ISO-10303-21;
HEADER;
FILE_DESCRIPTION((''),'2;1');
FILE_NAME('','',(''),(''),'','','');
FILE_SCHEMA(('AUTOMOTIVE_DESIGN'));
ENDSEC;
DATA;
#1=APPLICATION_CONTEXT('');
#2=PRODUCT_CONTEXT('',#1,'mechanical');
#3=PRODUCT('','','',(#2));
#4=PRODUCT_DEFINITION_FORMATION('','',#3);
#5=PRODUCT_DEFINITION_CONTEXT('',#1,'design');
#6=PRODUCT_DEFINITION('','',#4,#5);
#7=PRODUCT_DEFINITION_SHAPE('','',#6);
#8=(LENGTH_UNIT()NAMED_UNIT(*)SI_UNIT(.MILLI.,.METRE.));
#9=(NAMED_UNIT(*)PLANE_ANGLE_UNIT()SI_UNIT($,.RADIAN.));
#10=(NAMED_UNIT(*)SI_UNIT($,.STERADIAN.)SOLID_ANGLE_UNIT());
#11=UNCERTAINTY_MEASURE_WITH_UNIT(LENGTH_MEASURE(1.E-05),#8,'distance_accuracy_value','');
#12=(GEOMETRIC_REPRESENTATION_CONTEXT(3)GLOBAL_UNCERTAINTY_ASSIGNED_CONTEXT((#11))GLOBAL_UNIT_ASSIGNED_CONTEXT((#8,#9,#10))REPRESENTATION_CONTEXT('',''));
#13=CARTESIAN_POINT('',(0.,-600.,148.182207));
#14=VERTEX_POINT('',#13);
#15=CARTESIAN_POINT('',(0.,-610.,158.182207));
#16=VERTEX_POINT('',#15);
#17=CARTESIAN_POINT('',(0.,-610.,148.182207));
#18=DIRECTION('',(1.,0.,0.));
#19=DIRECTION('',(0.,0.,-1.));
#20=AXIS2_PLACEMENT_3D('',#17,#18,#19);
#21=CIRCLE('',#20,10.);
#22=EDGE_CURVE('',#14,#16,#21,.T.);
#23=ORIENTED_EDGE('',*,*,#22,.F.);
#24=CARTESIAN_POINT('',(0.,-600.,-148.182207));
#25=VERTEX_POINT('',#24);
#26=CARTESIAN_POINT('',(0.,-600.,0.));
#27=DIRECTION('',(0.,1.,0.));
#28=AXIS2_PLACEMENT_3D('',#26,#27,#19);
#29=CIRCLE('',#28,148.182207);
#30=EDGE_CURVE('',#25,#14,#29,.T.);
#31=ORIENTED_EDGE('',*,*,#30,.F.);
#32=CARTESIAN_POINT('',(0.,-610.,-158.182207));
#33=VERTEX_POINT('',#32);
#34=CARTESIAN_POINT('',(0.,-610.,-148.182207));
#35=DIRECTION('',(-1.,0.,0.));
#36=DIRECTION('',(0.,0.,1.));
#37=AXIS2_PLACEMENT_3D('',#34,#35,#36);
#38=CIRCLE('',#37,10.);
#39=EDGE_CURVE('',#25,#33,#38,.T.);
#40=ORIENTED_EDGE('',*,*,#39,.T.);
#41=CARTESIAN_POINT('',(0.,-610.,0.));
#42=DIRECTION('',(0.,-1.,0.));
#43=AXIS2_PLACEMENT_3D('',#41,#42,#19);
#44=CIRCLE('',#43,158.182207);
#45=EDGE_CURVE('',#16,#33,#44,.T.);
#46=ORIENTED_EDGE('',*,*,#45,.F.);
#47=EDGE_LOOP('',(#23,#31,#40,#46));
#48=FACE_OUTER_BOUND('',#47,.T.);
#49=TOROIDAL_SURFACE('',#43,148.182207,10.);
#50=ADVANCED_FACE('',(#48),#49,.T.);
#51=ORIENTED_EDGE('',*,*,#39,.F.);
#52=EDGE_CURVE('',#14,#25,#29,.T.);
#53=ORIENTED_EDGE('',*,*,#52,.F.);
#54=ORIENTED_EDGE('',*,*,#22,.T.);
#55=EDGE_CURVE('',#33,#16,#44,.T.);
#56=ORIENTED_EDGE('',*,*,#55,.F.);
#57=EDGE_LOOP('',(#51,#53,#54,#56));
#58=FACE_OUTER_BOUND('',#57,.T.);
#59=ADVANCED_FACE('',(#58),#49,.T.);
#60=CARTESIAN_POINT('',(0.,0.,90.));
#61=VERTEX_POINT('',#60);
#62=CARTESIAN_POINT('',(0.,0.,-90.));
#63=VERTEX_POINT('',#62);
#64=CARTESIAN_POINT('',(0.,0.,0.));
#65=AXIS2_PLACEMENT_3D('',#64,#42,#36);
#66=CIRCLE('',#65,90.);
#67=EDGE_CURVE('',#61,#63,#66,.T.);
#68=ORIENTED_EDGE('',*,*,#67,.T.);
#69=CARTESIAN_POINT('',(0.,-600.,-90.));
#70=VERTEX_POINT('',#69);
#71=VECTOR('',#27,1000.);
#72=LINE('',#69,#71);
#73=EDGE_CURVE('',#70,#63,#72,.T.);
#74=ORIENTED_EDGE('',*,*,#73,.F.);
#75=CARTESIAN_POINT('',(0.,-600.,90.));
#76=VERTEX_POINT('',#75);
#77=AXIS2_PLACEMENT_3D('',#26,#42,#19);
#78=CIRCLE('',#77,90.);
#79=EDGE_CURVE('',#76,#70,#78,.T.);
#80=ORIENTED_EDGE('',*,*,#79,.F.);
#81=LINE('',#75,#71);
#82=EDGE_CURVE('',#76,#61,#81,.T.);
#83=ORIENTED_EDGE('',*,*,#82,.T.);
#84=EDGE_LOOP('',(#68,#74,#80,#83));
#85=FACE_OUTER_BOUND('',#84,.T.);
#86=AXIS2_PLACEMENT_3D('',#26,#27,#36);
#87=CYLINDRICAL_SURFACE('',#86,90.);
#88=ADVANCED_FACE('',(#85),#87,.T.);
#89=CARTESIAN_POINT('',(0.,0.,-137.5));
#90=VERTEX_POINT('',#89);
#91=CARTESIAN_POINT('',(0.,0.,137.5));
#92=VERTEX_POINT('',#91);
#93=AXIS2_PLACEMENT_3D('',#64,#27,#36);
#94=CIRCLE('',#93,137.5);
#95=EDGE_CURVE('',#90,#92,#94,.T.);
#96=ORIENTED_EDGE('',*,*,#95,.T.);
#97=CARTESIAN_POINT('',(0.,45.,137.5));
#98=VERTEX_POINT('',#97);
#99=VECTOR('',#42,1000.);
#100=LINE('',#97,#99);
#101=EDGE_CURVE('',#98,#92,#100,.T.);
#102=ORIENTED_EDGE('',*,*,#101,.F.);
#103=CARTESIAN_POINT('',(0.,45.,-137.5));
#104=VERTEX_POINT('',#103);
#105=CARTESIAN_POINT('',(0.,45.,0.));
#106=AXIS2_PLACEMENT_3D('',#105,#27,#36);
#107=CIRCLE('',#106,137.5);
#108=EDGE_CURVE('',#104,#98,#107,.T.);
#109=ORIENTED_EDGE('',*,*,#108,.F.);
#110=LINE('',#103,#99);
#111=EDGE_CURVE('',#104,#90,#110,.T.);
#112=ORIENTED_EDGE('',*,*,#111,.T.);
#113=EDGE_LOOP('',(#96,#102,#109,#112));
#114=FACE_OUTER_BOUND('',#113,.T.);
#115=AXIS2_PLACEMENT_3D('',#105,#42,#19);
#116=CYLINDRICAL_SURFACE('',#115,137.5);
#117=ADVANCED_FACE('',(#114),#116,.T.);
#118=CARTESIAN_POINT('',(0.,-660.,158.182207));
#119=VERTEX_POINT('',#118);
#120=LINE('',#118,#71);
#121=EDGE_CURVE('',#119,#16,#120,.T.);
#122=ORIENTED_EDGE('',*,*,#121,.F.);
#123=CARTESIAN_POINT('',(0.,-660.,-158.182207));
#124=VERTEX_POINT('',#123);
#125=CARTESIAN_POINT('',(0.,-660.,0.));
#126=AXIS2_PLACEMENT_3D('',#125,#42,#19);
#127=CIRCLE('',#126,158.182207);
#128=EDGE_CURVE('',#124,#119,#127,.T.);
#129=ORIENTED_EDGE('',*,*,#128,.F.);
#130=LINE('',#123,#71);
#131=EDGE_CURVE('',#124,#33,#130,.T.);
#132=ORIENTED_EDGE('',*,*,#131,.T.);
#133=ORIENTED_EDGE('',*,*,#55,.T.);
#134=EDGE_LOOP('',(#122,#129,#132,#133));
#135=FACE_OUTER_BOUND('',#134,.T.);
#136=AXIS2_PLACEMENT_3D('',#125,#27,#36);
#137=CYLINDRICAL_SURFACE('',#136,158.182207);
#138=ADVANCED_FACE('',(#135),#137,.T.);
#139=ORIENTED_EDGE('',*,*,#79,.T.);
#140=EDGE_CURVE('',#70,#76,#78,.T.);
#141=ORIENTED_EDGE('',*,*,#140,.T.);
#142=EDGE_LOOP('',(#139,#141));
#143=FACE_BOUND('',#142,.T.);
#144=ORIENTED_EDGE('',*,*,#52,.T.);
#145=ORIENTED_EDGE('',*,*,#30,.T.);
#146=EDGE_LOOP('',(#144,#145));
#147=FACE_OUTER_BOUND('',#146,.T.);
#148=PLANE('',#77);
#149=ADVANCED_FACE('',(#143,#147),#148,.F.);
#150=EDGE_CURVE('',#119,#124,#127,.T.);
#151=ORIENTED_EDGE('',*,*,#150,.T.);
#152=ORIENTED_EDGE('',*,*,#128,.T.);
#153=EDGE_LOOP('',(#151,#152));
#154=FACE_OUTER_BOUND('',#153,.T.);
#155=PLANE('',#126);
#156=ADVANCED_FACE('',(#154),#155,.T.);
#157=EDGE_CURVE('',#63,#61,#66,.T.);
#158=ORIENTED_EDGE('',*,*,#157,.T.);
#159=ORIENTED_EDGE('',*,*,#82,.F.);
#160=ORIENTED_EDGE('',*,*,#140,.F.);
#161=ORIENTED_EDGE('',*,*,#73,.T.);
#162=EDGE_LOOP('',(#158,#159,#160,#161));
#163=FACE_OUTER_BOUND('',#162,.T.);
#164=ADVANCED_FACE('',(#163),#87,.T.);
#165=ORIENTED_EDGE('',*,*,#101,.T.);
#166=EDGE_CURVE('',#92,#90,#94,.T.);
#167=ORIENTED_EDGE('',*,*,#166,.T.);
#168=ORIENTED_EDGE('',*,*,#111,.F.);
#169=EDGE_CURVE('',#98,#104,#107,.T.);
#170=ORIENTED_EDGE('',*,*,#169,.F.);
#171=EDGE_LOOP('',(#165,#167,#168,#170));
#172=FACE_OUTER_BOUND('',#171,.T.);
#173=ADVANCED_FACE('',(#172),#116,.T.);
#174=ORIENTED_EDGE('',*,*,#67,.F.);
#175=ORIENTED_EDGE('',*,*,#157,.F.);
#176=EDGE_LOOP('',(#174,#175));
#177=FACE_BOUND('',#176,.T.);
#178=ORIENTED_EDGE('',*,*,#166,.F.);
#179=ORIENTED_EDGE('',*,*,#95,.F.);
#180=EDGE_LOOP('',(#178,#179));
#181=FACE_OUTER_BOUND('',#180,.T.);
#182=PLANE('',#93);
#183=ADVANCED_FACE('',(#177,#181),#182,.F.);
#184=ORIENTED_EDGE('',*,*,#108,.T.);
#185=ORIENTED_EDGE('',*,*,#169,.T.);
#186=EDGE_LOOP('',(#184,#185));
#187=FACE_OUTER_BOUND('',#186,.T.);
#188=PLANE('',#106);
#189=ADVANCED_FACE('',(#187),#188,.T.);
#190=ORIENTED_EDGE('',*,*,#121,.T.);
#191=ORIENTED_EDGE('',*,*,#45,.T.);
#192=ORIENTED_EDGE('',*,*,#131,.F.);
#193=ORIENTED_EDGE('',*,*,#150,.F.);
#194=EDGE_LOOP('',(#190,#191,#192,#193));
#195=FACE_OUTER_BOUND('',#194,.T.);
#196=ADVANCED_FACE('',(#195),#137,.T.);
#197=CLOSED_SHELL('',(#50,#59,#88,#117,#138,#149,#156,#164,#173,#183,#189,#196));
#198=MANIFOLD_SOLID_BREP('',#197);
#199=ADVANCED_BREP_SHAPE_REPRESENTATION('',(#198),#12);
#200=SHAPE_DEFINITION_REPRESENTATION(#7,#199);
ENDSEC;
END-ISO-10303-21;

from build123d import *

# Parameters (mm, degrees)
SKETCH1_R           = 137.5
BOSS_EXTRUDE1_DEPTH = 45
SKETCH2_R           = 90
BOSS_EXTRUDE2_DEPTH = 600
SKETCH3_R           = 158.18220737
BOSS_EXTRUDE3_DEPTH = 60
FILLET1_R           = 10


with BuildPart() as part:
    # Sketch1 → Boss-Extrude1 (new body)
    with BuildSketch(Plane(origin=(0, 0, 0), x_dir=(1, 0, 0), z_dir=(0, 1, 0))):
        with Locations(Location((0, 0, 0), (0, 0, 270))):
            Circle(SKETCH1_R)
    extrude(amount=BOSS_EXTRUDE1_DEPTH)

    # Sketch2 → Boss-Extrude2 (add)
    with BuildSketch(Plane.XZ):
        with Locations(Location((0, 0, 0), (0, 0, 90))):
            Circle(SKETCH2_R)
    extrude(amount=BOSS_EXTRUDE2_DEPTH)

    # Sketch3 → Boss-Extrude3 (add)
    with BuildSketch(Plane.XZ.offset(600)):
        with Locations(Location((0, 0, 0), (0, 0, 270))):
            Circle(SKETCH3_R)
    extrude(amount=BOSS_EXTRUDE3_DEPTH)

    # Fillet1
    fillet1_edges = [part.edges().sort_by_distance(p)[0] for p in [
        (0, -600, 158.18220737),
    ]]
    fillet(fillet1_edges, radius=FILLET1_R)


solid = part.part
